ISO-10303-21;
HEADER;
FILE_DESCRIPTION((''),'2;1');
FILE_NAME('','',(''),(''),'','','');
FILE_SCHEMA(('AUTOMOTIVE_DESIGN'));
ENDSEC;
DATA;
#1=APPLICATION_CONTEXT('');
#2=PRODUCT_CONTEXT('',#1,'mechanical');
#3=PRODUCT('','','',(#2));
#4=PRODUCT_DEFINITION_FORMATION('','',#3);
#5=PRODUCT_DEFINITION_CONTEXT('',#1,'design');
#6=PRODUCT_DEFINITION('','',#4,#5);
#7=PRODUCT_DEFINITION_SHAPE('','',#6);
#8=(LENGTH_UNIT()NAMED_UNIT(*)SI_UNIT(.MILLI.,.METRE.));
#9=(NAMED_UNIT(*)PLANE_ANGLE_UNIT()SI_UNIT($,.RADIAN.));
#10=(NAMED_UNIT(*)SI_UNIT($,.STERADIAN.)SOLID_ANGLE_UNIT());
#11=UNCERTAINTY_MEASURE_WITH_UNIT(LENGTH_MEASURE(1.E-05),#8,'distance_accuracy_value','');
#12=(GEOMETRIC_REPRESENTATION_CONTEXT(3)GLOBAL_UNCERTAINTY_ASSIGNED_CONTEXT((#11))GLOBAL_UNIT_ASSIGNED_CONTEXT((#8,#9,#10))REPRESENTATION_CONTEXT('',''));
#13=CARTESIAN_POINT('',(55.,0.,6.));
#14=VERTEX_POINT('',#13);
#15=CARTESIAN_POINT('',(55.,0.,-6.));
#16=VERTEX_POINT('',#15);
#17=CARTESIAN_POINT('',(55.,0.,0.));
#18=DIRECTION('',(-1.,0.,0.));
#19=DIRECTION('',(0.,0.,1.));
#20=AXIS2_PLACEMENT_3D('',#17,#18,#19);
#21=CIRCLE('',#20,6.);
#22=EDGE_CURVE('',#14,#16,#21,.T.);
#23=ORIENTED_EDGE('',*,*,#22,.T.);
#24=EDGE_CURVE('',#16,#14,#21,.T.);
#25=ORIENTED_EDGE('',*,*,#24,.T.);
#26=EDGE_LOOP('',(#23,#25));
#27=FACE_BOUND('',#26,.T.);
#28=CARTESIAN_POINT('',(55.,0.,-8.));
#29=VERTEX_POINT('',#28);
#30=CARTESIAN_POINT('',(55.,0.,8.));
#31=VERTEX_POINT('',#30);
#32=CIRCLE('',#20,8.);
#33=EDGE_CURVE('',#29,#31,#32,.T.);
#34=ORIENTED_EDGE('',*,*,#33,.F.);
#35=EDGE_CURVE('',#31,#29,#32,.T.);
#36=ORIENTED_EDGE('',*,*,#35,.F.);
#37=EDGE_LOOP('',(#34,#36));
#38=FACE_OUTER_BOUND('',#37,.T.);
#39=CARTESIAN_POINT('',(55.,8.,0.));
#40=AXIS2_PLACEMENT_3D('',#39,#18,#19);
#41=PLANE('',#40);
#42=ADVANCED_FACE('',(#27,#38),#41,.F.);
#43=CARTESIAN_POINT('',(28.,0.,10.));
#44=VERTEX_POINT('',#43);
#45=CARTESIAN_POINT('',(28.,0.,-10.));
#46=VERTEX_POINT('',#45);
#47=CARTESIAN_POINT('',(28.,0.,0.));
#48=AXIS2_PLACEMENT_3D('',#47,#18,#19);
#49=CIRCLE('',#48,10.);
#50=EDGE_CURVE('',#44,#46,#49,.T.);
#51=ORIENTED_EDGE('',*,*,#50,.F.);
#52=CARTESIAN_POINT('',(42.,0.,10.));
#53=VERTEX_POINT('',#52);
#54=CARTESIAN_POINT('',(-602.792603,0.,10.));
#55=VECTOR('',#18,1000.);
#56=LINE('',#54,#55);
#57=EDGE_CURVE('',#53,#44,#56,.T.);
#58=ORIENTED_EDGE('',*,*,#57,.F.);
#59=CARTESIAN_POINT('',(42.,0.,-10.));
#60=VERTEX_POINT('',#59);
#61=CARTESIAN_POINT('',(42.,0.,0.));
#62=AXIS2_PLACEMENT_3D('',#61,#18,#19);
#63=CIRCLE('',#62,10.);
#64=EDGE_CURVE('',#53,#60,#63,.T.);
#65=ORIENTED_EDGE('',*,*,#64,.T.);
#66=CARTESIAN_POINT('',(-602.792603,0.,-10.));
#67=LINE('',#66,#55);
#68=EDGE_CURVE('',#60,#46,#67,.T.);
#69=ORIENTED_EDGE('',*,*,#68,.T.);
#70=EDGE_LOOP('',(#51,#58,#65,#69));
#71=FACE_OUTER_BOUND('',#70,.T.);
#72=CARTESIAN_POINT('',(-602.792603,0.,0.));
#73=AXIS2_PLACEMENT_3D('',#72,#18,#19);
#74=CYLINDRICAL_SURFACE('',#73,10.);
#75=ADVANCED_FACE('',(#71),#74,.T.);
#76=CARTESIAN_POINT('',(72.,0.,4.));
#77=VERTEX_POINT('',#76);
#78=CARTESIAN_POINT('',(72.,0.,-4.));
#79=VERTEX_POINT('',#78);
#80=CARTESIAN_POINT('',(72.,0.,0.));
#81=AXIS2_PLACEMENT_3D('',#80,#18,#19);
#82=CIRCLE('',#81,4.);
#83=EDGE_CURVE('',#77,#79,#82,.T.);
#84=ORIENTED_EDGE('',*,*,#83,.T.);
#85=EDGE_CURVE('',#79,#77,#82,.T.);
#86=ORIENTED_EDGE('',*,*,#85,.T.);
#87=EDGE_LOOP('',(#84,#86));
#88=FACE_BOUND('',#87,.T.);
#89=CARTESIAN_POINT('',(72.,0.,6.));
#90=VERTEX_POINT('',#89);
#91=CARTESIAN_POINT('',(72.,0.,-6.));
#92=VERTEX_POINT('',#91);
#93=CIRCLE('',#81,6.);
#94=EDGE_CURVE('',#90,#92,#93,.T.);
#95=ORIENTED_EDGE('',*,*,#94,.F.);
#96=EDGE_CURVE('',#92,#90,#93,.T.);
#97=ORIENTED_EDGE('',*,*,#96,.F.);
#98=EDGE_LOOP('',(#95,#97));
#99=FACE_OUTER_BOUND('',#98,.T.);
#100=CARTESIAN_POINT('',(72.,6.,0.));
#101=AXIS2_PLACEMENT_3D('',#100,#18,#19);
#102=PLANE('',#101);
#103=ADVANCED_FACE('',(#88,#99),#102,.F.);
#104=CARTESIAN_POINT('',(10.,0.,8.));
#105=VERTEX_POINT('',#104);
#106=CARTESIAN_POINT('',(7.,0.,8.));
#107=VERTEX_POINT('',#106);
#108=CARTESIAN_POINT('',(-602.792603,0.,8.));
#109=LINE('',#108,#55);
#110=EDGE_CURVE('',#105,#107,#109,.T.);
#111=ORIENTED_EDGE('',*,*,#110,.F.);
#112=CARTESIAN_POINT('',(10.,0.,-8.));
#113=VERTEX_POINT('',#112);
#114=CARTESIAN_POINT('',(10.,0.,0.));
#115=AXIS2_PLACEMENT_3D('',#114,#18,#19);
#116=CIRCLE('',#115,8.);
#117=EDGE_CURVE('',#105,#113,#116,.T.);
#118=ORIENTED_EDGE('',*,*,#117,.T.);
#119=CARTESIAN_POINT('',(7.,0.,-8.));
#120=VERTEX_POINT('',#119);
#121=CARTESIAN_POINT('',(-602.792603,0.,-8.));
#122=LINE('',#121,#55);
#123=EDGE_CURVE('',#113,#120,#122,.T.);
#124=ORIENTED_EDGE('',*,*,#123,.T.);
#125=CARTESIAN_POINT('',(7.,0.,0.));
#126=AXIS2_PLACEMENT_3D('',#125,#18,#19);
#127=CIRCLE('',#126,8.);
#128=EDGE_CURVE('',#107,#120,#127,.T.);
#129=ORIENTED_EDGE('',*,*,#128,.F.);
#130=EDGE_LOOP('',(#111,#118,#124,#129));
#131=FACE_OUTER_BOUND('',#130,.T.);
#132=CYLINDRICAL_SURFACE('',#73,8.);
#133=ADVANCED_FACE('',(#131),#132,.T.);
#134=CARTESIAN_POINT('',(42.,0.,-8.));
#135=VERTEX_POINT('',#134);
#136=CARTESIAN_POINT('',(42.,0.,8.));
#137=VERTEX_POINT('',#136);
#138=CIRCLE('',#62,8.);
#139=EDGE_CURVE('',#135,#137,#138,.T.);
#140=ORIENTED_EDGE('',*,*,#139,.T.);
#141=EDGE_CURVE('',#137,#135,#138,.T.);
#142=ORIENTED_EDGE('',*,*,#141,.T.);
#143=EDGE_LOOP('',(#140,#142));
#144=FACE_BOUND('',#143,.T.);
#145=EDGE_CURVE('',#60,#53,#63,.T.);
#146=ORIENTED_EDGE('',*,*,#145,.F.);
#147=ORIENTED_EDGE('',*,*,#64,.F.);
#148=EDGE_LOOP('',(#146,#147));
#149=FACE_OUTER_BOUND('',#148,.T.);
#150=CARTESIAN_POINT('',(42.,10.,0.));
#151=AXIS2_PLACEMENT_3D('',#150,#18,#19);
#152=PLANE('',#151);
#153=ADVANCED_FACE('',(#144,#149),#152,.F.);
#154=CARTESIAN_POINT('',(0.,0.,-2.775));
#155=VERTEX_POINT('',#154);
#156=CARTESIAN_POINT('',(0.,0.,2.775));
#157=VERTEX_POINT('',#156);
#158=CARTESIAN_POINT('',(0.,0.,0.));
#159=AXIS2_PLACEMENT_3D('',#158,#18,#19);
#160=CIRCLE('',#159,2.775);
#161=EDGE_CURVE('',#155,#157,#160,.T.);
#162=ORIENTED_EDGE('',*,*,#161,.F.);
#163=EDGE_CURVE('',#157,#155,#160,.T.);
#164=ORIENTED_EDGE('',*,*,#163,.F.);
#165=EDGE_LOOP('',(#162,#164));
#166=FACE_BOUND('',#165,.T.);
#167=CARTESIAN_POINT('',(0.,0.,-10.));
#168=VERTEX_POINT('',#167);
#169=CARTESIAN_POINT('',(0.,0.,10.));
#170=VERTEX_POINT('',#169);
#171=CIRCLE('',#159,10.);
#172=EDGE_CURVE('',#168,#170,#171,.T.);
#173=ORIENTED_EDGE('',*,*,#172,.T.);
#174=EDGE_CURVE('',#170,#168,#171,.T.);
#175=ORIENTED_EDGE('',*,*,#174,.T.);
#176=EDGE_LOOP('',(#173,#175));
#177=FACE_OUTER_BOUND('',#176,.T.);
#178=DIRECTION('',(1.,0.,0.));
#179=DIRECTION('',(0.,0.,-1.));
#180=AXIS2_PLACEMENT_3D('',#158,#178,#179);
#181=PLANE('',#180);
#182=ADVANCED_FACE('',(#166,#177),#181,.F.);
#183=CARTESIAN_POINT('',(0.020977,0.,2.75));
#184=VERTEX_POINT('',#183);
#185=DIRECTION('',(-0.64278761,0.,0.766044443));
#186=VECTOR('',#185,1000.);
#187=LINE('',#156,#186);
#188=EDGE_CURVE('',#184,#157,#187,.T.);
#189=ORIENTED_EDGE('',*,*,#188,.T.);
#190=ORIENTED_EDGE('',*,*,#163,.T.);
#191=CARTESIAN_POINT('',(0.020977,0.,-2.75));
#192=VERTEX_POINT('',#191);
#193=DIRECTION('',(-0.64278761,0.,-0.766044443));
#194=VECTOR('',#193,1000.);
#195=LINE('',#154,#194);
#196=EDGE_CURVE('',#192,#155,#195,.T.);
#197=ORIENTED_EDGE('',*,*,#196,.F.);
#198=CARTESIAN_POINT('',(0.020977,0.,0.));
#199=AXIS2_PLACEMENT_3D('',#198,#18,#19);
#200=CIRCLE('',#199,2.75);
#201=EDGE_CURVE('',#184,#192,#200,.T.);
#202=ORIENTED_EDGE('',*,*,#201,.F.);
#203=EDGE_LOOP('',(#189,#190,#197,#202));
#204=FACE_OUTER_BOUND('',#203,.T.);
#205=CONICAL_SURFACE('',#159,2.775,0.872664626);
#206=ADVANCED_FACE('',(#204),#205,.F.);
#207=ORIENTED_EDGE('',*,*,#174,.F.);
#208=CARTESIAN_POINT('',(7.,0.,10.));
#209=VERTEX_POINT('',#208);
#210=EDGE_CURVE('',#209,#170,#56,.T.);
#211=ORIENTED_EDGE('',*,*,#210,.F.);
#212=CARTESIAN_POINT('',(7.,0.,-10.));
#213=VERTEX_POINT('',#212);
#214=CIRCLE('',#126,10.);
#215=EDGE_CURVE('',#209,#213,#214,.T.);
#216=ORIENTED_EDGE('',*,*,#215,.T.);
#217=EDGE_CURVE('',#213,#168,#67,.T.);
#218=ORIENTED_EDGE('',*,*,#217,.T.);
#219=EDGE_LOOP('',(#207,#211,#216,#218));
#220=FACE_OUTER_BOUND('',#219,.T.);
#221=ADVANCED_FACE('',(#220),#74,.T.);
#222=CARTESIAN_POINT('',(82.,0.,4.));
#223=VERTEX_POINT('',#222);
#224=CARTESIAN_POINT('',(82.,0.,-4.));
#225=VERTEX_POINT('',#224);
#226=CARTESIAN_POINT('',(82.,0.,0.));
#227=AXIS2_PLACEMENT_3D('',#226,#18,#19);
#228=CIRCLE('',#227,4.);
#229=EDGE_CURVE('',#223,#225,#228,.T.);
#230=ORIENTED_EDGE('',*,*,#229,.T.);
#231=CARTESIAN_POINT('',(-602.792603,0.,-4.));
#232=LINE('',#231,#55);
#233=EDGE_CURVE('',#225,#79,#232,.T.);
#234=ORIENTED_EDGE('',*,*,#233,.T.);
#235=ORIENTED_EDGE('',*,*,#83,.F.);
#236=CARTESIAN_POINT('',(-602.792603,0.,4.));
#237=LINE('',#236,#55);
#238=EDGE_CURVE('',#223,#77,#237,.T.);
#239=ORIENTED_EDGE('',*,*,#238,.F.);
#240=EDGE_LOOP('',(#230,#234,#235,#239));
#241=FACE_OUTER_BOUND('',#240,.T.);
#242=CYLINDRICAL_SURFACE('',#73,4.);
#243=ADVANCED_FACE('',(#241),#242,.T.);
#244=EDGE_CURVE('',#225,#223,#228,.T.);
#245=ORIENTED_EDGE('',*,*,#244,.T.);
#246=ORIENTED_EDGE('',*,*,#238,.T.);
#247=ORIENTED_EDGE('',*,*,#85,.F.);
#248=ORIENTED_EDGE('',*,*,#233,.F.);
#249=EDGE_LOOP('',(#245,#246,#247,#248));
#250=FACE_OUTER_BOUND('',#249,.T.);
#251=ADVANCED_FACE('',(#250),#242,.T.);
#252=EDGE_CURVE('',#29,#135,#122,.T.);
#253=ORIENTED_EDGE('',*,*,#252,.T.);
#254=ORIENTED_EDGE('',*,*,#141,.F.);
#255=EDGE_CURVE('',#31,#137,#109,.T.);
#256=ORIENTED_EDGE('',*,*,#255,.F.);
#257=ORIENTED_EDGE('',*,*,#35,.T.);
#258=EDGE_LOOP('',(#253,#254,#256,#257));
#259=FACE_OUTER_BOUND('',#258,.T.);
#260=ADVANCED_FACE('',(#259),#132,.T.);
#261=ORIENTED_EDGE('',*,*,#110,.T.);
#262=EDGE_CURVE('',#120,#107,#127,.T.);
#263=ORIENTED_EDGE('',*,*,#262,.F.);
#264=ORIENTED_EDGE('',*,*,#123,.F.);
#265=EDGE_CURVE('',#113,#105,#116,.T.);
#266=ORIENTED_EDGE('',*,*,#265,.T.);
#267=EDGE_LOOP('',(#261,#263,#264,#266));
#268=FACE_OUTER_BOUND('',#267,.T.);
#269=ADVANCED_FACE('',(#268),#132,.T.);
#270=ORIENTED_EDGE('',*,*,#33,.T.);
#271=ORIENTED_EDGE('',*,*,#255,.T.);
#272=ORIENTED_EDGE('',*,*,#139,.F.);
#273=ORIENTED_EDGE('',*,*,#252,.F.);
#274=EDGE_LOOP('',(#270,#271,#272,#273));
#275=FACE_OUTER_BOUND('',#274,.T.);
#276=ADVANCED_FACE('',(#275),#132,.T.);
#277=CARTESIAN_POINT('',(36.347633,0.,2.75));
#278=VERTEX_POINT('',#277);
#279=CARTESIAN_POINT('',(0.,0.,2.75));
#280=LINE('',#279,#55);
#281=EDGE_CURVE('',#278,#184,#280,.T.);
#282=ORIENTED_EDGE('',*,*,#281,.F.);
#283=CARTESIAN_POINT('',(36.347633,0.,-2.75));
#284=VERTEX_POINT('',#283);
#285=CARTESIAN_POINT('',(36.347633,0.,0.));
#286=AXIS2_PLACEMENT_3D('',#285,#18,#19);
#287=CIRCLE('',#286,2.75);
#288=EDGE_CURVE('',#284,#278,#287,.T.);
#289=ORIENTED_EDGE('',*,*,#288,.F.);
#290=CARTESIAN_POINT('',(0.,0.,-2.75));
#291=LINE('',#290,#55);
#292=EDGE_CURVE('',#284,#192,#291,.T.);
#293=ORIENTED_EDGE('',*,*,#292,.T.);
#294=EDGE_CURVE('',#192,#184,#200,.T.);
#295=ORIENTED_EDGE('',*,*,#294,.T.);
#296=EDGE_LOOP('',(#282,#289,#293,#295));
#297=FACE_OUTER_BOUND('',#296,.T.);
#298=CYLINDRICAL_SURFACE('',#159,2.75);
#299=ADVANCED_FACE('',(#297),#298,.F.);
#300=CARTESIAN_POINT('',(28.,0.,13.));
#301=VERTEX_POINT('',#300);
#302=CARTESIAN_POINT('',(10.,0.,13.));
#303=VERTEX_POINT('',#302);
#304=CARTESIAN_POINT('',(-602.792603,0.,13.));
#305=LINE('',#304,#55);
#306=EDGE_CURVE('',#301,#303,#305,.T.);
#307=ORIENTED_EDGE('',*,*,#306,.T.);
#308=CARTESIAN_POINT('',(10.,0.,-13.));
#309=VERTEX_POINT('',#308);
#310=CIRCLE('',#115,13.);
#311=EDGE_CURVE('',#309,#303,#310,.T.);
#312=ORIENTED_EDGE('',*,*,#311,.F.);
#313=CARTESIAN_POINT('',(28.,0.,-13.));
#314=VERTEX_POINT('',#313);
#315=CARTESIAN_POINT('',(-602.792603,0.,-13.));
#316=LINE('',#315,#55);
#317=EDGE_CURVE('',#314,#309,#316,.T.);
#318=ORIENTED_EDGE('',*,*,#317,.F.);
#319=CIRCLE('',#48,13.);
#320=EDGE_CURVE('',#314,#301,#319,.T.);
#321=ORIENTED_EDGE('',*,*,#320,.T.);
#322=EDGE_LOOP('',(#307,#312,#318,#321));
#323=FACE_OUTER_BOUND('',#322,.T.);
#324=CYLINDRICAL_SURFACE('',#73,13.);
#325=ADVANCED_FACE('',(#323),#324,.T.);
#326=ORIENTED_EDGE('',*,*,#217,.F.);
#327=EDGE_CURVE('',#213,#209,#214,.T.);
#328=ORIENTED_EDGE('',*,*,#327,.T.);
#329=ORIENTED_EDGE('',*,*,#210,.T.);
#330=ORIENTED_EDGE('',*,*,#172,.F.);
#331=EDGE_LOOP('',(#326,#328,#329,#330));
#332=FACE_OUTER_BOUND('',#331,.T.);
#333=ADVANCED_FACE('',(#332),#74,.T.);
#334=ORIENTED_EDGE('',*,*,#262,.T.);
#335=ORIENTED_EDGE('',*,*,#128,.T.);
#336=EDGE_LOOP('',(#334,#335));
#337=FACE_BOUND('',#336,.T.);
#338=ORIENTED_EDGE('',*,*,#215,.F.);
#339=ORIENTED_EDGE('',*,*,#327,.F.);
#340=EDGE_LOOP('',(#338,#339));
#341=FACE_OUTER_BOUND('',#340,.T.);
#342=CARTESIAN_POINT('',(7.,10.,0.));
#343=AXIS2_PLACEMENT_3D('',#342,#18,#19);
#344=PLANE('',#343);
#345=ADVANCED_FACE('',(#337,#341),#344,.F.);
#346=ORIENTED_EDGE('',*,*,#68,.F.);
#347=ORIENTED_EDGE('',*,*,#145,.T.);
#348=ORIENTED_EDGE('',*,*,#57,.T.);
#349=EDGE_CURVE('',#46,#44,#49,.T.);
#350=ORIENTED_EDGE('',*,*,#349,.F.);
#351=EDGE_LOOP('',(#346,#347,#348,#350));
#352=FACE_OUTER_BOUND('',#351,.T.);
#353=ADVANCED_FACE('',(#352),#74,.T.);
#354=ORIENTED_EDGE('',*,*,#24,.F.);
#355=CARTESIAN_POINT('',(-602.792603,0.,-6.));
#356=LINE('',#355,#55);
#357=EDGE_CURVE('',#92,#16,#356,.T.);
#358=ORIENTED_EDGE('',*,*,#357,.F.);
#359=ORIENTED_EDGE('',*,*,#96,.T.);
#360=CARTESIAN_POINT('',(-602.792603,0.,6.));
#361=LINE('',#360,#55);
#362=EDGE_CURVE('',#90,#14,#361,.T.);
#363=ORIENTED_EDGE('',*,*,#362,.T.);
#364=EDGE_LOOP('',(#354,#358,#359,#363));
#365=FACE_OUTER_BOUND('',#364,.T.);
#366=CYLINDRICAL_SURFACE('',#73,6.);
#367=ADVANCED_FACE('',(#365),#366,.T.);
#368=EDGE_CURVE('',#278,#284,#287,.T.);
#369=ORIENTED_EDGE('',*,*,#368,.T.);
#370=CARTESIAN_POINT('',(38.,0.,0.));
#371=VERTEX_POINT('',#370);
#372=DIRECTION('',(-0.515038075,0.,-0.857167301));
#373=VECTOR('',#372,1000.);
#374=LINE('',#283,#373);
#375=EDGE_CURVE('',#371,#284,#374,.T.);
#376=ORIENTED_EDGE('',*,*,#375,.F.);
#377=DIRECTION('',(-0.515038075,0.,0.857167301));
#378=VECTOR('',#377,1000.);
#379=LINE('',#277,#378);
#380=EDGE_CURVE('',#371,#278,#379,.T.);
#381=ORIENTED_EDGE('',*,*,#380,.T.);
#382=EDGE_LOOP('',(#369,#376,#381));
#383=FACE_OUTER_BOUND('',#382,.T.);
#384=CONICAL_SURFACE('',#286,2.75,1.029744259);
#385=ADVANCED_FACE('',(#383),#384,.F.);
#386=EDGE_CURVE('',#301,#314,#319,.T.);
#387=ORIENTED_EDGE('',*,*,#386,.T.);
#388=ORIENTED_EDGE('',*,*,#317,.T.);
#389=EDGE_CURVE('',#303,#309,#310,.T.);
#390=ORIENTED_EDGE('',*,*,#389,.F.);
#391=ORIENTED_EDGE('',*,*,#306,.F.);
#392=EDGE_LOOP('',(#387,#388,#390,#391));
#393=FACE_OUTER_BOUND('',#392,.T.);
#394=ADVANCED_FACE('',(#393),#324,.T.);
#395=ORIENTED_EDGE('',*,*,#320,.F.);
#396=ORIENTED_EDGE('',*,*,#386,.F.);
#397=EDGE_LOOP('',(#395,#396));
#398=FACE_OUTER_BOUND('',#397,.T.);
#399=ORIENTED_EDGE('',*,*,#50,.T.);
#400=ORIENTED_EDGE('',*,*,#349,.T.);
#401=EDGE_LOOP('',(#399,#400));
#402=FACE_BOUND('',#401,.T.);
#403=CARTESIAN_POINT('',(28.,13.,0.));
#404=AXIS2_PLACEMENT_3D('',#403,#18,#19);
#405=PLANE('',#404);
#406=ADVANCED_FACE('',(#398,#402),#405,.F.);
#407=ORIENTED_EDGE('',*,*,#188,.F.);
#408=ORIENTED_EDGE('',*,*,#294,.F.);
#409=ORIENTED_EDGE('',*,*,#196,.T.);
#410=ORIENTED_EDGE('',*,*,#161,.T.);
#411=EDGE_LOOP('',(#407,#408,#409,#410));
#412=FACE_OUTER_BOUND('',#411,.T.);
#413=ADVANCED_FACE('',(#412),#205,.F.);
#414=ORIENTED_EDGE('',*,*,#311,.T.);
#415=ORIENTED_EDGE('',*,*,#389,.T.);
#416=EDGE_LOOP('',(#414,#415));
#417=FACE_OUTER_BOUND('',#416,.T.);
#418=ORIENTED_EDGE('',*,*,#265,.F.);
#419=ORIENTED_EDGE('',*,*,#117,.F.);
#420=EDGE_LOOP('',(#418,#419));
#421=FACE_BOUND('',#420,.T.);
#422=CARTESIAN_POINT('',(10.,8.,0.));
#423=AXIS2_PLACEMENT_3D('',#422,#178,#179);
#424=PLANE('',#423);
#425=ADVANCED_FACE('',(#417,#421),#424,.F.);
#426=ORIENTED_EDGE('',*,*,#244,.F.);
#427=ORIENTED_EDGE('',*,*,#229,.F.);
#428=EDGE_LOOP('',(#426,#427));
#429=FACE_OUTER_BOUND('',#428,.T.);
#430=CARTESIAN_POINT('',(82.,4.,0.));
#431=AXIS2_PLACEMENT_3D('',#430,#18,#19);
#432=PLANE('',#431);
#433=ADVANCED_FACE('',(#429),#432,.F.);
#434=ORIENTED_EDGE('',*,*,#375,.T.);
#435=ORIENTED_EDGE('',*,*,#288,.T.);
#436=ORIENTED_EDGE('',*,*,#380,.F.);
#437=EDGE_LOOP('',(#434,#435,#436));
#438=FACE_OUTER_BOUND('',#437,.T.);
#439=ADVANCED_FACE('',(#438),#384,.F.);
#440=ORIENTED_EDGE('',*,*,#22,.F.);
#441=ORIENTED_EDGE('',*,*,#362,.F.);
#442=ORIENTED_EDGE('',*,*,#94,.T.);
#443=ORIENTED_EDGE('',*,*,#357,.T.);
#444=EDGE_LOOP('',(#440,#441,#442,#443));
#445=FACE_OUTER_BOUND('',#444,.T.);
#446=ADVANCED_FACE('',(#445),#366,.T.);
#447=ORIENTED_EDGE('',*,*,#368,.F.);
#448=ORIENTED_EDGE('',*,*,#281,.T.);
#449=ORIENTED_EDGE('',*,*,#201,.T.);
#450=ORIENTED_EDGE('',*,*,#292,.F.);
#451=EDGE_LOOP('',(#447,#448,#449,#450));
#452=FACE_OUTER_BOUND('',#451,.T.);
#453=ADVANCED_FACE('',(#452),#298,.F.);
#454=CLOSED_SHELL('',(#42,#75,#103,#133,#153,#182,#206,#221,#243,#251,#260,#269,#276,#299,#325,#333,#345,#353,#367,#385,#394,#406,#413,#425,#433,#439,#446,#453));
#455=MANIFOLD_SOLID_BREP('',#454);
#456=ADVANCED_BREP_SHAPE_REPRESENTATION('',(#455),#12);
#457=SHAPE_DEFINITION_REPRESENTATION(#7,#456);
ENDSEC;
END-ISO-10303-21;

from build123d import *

# Parameters (mm, degrees)
AXIAL_HOLE_M5_CLEARANCE_D           = 5.5
AXIAL_HOLE_M5_CLEARANCE_DEPTH       = 36.347633298
AXIAL_HOLE_M5_CLEARANCE_CSINK_D     = 5.55
AXIAL_HOLE_M5_CLEARANCE_CSINK_ANGLE = 100
AXIAL_HOLE_M5_CLEARANCE_TIP         = 1.652366702


with BuildPart() as part:
    # Shaft Profile Sketch → Stepped Shaft Revolve (revolve)
    with BuildSketch(Plane.XY, mode=Mode.PRIVATE) as stepped_shaft_revolve_sk:
        Polygon((0, 0), (0, 10), (7, 10), (7, 8), (10, 8), (10, 13), (28, 13), (28, 10), (42, 10), (42, 8), (55, 8), (55, 6), (72, 6), (72, 4), (82, 4), (82, 0), align=None)
    revolve(stepped_shaft_revolve_sk.sketch.rotate(Axis((-602.792603174, 0, 0), (1, 0, 0)), 90), axis=Axis((-602.792603174, 0, 0), (1, 0, 0)))

    # Axial Hole M5 Clearance
    with Locations(Plane(origin=(0, 0, 0), x_dir=(0, 0, -1), z_dir=(-1, 0, 0))):
        with Locations((0, 0)):
            CounterSinkHole(AXIAL_HOLE_M5_CLEARANCE_D / 2, AXIAL_HOLE_M5_CLEARANCE_CSINK_D / 2, depth=AXIAL_HOLE_M5_CLEARANCE_DEPTH, counter_sink_angle=AXIAL_HOLE_M5_CLEARANCE_CSINK_ANGLE)
            with Locations((0, 0, -(AXIAL_HOLE_M5_CLEARANCE_DEPTH + AXIAL_HOLE_M5_CLEARANCE_TIP / 2))):  # 118° drill point
                Cone(0, AXIAL_HOLE_M5_CLEARANCE_D / 2, AXIAL_HOLE_M5_CLEARANCE_TIP, mode=Mode.SUBTRACT)


solid = part.part
